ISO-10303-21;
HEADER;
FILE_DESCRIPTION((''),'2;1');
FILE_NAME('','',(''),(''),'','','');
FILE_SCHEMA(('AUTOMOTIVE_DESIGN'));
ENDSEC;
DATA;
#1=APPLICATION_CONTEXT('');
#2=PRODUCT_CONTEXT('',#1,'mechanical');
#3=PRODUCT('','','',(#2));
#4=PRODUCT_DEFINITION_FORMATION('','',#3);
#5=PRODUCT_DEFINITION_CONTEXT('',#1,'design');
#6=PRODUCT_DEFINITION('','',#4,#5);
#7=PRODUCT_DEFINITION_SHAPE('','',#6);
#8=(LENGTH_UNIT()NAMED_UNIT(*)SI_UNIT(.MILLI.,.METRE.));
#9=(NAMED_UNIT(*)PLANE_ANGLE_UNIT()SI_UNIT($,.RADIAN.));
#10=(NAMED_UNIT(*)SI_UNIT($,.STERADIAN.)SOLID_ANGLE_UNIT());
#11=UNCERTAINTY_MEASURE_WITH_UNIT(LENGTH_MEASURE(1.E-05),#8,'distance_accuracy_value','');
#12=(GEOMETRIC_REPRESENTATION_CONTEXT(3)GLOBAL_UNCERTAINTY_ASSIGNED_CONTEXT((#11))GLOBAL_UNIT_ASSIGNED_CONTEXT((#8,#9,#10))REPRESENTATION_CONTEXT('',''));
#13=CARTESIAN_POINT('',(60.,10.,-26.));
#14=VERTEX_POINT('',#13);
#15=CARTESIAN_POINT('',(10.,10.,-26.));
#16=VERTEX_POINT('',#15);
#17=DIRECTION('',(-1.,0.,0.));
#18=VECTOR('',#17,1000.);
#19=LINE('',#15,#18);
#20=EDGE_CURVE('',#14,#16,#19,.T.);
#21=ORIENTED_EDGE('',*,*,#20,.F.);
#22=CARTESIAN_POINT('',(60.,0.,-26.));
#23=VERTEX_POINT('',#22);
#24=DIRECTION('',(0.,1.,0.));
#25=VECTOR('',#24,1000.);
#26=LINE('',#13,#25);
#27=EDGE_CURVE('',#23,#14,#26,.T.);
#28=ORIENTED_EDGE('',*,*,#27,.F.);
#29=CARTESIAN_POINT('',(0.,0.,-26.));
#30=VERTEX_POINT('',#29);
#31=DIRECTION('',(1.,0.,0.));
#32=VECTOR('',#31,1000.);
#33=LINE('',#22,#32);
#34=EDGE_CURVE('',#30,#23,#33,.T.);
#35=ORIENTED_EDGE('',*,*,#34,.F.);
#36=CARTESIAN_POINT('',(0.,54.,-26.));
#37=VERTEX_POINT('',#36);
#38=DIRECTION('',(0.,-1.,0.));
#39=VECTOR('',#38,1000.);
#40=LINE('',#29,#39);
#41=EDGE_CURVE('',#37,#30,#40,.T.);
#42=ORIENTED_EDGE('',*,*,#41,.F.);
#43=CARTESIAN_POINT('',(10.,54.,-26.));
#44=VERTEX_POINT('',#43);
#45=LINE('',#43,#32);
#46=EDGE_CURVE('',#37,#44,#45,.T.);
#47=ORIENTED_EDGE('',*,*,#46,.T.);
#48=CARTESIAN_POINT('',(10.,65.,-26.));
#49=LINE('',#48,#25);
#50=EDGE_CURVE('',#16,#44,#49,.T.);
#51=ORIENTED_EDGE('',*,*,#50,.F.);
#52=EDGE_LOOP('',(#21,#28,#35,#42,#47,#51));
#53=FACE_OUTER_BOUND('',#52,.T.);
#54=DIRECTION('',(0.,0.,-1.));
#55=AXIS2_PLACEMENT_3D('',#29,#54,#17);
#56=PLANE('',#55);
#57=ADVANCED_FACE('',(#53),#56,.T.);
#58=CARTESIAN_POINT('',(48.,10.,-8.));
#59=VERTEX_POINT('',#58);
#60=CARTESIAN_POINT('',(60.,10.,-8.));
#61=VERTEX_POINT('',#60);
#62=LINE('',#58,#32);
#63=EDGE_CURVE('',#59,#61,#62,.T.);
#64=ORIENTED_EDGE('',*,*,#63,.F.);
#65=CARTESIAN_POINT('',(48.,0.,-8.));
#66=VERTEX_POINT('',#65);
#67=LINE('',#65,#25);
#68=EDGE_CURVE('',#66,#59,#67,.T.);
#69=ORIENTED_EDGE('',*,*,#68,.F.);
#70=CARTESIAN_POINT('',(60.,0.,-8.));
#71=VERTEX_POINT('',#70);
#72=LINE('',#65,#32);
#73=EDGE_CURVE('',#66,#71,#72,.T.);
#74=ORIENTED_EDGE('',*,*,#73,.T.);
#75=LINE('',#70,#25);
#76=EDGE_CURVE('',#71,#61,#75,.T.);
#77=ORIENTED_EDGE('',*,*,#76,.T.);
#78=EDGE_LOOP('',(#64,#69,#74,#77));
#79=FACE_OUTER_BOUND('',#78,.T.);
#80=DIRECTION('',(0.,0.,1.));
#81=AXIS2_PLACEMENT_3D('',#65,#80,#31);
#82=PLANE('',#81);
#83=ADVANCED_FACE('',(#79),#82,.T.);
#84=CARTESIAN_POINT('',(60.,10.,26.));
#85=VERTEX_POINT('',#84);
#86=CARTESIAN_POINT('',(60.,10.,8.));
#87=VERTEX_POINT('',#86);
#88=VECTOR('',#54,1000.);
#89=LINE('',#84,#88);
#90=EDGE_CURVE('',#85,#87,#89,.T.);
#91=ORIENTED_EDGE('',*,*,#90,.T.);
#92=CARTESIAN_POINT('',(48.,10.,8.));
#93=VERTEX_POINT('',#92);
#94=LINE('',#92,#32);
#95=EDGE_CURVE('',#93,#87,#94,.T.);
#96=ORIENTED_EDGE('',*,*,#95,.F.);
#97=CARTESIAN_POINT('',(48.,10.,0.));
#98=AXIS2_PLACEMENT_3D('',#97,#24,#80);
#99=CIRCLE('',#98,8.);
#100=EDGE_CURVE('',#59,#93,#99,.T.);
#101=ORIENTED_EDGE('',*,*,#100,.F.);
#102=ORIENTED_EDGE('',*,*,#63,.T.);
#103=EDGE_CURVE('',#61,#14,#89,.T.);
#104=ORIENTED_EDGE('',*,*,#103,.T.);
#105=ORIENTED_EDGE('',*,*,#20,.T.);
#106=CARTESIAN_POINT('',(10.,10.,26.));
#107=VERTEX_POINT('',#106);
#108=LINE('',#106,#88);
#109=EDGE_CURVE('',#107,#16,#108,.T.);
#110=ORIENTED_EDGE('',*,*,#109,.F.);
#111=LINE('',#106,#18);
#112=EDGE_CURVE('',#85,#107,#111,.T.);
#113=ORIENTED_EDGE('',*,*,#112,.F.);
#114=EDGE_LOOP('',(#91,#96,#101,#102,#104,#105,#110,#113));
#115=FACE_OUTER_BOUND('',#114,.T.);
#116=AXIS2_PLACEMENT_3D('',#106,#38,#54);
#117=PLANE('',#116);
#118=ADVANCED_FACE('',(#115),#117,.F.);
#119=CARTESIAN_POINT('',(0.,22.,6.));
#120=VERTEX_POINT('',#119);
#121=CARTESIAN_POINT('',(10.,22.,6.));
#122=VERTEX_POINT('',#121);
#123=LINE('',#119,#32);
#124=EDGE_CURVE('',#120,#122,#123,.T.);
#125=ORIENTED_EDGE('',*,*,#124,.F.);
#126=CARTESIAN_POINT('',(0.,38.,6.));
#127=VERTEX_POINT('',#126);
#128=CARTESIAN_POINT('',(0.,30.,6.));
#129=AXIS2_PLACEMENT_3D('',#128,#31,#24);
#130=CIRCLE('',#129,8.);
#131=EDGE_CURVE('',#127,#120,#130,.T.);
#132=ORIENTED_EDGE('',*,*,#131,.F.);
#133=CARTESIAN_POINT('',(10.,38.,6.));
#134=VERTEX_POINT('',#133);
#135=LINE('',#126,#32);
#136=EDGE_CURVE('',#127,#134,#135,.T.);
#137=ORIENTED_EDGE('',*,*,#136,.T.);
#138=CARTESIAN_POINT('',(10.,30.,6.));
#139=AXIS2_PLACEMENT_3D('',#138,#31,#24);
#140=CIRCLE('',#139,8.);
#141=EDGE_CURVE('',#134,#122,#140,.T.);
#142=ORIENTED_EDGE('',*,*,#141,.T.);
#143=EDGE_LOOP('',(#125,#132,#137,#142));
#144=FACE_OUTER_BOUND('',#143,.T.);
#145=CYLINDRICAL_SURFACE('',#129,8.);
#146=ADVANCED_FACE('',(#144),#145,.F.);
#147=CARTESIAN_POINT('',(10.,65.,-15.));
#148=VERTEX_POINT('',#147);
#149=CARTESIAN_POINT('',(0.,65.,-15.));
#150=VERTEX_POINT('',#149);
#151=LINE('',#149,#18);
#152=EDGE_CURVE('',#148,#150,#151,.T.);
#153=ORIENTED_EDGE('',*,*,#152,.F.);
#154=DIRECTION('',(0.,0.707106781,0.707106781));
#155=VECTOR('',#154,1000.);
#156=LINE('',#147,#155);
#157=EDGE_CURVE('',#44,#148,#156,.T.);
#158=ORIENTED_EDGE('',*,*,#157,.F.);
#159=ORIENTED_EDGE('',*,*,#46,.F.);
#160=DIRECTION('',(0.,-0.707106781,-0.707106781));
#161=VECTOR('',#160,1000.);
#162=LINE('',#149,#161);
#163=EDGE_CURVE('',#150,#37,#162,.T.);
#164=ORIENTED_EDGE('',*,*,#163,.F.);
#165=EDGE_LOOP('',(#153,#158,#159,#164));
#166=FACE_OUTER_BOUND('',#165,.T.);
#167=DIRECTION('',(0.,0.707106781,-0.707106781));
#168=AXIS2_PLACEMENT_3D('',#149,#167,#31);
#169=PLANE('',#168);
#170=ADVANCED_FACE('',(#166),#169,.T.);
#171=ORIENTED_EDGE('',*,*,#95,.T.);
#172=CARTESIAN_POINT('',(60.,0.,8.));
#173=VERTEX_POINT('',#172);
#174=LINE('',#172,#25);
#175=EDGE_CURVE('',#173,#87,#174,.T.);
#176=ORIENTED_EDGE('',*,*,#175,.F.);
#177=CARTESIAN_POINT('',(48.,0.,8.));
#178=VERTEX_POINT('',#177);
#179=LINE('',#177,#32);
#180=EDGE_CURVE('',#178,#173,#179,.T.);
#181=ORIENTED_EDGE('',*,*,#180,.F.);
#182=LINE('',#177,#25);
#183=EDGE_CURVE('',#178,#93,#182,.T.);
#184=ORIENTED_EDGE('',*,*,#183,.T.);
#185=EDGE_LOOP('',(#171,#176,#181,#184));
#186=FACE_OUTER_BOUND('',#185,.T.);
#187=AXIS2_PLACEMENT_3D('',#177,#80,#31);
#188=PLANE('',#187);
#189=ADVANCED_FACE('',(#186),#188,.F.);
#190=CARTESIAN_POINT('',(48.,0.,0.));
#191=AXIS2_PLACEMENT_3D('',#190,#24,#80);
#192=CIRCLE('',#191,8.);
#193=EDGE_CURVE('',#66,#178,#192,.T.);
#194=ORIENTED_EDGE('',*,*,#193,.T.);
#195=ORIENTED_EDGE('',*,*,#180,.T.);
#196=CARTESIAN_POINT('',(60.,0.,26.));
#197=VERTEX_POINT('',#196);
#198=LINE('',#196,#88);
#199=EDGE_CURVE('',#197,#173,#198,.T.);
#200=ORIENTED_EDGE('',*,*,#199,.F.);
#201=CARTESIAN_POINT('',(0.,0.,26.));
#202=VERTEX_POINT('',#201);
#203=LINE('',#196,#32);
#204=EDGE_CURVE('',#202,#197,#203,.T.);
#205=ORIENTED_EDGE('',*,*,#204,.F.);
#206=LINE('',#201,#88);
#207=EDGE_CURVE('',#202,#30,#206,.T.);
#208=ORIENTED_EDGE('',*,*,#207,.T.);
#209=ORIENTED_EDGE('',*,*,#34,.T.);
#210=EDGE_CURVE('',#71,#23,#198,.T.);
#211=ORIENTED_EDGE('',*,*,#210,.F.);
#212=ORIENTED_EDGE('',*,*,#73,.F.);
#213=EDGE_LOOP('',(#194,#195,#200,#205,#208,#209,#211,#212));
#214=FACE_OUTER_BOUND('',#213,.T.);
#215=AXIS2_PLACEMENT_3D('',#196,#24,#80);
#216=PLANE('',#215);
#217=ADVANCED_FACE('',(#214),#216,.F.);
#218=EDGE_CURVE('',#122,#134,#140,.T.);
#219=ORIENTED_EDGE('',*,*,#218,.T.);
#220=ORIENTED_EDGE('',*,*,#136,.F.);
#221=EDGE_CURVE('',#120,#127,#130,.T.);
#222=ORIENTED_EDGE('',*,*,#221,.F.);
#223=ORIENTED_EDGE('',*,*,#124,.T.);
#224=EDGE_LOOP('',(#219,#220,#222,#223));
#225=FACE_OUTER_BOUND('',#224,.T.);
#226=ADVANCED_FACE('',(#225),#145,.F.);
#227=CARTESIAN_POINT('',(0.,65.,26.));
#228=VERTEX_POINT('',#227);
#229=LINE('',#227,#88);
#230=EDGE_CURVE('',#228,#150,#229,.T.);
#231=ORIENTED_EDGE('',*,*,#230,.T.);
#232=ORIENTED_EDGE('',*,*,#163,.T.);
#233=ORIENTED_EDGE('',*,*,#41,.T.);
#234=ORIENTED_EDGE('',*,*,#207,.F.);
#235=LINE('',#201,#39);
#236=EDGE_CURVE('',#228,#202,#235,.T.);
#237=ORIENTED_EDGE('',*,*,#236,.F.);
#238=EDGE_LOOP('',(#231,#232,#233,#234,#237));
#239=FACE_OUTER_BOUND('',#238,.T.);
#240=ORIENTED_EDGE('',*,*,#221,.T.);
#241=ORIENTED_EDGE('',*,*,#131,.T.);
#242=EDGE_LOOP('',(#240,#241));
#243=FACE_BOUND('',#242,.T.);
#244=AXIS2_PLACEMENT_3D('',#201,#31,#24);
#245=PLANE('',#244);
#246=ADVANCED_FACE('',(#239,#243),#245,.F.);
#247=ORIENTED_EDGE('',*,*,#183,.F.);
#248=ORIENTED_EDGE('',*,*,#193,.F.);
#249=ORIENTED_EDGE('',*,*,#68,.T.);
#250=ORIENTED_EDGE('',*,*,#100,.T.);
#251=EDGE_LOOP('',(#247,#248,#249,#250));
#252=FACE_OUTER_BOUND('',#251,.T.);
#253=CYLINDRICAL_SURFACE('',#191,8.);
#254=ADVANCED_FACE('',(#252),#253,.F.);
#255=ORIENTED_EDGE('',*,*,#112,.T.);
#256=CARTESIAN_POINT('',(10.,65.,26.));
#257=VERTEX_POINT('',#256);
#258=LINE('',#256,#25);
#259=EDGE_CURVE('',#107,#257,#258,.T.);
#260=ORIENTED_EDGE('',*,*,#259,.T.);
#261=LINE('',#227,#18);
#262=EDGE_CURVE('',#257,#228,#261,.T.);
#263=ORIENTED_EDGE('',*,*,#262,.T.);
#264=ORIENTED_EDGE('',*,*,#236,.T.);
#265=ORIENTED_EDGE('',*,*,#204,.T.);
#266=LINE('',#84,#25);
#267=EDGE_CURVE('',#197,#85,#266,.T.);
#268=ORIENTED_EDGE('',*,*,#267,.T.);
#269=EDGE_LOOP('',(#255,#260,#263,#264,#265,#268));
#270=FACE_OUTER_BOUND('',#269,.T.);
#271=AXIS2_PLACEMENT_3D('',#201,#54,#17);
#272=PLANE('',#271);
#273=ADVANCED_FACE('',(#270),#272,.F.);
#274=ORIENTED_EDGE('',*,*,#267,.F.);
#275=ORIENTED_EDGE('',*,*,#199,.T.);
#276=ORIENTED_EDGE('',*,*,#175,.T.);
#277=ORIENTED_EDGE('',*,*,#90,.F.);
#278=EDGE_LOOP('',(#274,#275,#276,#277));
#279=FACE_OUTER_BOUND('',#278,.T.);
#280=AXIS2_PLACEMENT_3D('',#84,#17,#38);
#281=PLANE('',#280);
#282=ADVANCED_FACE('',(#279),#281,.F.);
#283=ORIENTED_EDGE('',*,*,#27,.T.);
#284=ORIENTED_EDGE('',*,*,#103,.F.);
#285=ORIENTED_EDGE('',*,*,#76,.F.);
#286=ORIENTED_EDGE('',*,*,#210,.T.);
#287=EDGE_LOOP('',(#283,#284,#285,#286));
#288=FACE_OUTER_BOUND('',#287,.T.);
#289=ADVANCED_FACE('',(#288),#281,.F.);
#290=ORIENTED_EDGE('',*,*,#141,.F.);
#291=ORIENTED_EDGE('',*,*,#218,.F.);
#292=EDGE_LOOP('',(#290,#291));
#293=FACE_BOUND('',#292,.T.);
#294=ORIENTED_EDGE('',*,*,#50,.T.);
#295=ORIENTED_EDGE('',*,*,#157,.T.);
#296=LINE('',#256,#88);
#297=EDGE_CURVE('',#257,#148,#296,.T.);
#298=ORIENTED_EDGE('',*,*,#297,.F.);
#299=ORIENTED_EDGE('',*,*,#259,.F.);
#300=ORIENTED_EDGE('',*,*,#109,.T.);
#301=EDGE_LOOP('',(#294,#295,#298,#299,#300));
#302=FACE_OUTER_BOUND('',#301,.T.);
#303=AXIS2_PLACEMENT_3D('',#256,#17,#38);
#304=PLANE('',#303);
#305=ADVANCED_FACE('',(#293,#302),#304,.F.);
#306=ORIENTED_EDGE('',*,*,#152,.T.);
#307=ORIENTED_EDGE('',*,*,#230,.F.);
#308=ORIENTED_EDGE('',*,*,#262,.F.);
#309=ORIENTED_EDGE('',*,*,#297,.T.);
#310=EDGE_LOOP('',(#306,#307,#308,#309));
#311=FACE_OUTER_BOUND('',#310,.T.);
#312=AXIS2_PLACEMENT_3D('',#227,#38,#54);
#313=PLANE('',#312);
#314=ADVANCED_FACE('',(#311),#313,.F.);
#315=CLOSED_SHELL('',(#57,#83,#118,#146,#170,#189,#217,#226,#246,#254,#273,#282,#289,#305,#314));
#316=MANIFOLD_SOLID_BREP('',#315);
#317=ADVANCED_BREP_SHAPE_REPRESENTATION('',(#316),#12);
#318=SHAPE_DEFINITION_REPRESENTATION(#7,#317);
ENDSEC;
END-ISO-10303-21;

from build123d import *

# Parameters (mm, degrees)
L_BRACKET_BODY_DEPTH  = 26
BASE_U_SLOT_DEPTH     = 86.44588931
UPRIGHT_HOLE_SKETCH_R = 8
UPRIGHT_HOLE_16_DEPTH = 87.029064856
CHAMFER_11X45_SIZE    = 11


with BuildPart() as part:
    # L-Profile Sketch → L-Bracket Body (new, symmetric)
    with BuildSketch(Plane.XY):
        Polygon((0, 0), (0, 65), (10, 65), (10, 10), (60, 10), (60, 0), align=None)
    extrude(amount=L_BRACKET_BODY_DEPTH, both=True)

    # Base Slot Sketch → Base U-Slot (cut, through all)
    with BuildSketch(Plane(origin=(0, 10, 0), x_dir=(1, 0, 0), z_dir=(0, 1, 0))):
        with BuildLine():
            Line((48, 8), (60, 8))
            Line((60, 8), (60, -8))
            Line((60, -8), (48, -8))
            ThreePointArc((48, -8), (40, 0), (48, 8))
        make_face()
    extrude(amount=-BASE_U_SLOT_DEPTH, mode=Mode.SUBTRACT)

    # Upright Hole Sketch → Upright Hole Ø16 (cut, through all)
    with BuildSketch(Plane(origin=(10, 0, 0), x_dir=(0, 0, -1), z_dir=(1, 0, 0))):
        with Locations(Location((-6, 30, 0), (0, 0, 90))):
            Circle(UPRIGHT_HOLE_SKETCH_R)
    extrude(amount=-UPRIGHT_HOLE_16_DEPTH, mode=Mode.SUBTRACT)

    # Chamfer 11x45°
    chamfer_11x45_edges = [part.edges().sort_by_distance(p)[0] for p in [
        (5, 65, -26),
    ]]
    chamfer(chamfer_11x45_edges, length=CHAMFER_11X45_SIZE)


solid = part.part
